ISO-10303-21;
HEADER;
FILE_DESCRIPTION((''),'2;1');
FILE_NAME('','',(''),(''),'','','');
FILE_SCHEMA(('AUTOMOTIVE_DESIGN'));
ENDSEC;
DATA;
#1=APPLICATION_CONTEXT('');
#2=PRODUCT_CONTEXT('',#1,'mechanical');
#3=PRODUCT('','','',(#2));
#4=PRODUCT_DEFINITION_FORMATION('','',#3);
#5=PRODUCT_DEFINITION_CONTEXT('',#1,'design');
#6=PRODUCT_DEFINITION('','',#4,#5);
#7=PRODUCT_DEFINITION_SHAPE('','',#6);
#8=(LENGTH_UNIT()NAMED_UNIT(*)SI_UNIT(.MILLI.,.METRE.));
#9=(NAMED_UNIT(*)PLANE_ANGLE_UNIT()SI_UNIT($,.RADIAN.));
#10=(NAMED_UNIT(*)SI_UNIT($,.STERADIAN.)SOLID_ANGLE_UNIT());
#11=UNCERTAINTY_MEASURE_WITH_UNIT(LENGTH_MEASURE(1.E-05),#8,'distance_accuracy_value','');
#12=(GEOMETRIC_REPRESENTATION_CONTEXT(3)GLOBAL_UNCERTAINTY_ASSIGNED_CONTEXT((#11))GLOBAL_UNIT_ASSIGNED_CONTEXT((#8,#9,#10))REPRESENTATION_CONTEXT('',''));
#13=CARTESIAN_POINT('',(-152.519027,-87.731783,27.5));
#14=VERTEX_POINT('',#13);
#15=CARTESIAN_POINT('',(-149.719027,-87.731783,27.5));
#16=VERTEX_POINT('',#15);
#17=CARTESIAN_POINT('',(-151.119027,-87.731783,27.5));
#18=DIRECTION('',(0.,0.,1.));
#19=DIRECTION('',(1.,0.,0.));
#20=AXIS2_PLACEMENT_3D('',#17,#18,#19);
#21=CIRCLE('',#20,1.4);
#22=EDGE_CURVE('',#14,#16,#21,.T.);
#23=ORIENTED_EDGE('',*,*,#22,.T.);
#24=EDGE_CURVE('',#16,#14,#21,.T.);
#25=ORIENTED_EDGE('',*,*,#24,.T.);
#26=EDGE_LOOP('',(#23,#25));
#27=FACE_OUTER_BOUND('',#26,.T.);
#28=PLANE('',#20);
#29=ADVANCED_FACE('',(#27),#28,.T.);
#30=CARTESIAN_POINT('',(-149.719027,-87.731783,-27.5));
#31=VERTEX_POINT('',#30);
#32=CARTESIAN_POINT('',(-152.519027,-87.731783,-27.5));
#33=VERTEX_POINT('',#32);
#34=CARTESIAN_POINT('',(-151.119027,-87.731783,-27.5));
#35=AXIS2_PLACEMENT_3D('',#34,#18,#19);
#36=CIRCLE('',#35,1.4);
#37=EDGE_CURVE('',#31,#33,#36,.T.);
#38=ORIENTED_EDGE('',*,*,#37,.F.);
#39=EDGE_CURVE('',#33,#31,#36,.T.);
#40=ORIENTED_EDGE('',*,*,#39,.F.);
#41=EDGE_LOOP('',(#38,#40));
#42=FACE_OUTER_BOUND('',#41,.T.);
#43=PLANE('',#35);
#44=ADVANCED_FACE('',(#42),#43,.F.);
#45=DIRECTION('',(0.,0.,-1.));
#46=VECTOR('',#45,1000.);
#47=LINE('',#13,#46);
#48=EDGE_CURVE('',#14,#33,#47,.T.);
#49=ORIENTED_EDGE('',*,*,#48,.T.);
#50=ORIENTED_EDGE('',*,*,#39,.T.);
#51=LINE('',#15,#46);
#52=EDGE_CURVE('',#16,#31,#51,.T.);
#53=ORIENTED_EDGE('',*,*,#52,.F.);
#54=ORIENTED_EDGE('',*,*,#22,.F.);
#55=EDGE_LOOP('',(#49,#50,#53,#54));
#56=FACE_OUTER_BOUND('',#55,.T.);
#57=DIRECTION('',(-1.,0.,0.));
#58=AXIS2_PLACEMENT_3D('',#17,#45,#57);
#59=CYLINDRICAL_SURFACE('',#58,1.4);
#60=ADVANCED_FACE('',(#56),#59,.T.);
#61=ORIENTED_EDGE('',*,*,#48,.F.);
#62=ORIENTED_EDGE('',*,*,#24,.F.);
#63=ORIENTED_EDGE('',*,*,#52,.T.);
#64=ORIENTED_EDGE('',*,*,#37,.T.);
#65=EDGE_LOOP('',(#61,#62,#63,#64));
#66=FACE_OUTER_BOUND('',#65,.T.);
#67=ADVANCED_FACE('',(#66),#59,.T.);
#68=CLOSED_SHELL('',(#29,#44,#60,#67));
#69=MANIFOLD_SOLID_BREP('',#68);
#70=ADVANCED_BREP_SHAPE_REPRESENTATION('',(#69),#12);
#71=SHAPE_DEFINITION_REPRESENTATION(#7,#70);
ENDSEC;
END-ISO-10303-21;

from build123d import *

# Parameters (mm, degrees)
SKETCH1_R           = 1.4
BOSS_EXTRUDE1_DEPTH = 27.5


with BuildPart() as part:
    # Sketch1 → Boss-Extrude1 (new, symmetric)
    with BuildSketch(Plane.XY):
        with Locations((-151.119026916, -87.731782697)):
            Circle(SKETCH1_R)
    extrude(amount=BOSS_EXTRUDE1_DEPTH, both=True)


solid = part.part
